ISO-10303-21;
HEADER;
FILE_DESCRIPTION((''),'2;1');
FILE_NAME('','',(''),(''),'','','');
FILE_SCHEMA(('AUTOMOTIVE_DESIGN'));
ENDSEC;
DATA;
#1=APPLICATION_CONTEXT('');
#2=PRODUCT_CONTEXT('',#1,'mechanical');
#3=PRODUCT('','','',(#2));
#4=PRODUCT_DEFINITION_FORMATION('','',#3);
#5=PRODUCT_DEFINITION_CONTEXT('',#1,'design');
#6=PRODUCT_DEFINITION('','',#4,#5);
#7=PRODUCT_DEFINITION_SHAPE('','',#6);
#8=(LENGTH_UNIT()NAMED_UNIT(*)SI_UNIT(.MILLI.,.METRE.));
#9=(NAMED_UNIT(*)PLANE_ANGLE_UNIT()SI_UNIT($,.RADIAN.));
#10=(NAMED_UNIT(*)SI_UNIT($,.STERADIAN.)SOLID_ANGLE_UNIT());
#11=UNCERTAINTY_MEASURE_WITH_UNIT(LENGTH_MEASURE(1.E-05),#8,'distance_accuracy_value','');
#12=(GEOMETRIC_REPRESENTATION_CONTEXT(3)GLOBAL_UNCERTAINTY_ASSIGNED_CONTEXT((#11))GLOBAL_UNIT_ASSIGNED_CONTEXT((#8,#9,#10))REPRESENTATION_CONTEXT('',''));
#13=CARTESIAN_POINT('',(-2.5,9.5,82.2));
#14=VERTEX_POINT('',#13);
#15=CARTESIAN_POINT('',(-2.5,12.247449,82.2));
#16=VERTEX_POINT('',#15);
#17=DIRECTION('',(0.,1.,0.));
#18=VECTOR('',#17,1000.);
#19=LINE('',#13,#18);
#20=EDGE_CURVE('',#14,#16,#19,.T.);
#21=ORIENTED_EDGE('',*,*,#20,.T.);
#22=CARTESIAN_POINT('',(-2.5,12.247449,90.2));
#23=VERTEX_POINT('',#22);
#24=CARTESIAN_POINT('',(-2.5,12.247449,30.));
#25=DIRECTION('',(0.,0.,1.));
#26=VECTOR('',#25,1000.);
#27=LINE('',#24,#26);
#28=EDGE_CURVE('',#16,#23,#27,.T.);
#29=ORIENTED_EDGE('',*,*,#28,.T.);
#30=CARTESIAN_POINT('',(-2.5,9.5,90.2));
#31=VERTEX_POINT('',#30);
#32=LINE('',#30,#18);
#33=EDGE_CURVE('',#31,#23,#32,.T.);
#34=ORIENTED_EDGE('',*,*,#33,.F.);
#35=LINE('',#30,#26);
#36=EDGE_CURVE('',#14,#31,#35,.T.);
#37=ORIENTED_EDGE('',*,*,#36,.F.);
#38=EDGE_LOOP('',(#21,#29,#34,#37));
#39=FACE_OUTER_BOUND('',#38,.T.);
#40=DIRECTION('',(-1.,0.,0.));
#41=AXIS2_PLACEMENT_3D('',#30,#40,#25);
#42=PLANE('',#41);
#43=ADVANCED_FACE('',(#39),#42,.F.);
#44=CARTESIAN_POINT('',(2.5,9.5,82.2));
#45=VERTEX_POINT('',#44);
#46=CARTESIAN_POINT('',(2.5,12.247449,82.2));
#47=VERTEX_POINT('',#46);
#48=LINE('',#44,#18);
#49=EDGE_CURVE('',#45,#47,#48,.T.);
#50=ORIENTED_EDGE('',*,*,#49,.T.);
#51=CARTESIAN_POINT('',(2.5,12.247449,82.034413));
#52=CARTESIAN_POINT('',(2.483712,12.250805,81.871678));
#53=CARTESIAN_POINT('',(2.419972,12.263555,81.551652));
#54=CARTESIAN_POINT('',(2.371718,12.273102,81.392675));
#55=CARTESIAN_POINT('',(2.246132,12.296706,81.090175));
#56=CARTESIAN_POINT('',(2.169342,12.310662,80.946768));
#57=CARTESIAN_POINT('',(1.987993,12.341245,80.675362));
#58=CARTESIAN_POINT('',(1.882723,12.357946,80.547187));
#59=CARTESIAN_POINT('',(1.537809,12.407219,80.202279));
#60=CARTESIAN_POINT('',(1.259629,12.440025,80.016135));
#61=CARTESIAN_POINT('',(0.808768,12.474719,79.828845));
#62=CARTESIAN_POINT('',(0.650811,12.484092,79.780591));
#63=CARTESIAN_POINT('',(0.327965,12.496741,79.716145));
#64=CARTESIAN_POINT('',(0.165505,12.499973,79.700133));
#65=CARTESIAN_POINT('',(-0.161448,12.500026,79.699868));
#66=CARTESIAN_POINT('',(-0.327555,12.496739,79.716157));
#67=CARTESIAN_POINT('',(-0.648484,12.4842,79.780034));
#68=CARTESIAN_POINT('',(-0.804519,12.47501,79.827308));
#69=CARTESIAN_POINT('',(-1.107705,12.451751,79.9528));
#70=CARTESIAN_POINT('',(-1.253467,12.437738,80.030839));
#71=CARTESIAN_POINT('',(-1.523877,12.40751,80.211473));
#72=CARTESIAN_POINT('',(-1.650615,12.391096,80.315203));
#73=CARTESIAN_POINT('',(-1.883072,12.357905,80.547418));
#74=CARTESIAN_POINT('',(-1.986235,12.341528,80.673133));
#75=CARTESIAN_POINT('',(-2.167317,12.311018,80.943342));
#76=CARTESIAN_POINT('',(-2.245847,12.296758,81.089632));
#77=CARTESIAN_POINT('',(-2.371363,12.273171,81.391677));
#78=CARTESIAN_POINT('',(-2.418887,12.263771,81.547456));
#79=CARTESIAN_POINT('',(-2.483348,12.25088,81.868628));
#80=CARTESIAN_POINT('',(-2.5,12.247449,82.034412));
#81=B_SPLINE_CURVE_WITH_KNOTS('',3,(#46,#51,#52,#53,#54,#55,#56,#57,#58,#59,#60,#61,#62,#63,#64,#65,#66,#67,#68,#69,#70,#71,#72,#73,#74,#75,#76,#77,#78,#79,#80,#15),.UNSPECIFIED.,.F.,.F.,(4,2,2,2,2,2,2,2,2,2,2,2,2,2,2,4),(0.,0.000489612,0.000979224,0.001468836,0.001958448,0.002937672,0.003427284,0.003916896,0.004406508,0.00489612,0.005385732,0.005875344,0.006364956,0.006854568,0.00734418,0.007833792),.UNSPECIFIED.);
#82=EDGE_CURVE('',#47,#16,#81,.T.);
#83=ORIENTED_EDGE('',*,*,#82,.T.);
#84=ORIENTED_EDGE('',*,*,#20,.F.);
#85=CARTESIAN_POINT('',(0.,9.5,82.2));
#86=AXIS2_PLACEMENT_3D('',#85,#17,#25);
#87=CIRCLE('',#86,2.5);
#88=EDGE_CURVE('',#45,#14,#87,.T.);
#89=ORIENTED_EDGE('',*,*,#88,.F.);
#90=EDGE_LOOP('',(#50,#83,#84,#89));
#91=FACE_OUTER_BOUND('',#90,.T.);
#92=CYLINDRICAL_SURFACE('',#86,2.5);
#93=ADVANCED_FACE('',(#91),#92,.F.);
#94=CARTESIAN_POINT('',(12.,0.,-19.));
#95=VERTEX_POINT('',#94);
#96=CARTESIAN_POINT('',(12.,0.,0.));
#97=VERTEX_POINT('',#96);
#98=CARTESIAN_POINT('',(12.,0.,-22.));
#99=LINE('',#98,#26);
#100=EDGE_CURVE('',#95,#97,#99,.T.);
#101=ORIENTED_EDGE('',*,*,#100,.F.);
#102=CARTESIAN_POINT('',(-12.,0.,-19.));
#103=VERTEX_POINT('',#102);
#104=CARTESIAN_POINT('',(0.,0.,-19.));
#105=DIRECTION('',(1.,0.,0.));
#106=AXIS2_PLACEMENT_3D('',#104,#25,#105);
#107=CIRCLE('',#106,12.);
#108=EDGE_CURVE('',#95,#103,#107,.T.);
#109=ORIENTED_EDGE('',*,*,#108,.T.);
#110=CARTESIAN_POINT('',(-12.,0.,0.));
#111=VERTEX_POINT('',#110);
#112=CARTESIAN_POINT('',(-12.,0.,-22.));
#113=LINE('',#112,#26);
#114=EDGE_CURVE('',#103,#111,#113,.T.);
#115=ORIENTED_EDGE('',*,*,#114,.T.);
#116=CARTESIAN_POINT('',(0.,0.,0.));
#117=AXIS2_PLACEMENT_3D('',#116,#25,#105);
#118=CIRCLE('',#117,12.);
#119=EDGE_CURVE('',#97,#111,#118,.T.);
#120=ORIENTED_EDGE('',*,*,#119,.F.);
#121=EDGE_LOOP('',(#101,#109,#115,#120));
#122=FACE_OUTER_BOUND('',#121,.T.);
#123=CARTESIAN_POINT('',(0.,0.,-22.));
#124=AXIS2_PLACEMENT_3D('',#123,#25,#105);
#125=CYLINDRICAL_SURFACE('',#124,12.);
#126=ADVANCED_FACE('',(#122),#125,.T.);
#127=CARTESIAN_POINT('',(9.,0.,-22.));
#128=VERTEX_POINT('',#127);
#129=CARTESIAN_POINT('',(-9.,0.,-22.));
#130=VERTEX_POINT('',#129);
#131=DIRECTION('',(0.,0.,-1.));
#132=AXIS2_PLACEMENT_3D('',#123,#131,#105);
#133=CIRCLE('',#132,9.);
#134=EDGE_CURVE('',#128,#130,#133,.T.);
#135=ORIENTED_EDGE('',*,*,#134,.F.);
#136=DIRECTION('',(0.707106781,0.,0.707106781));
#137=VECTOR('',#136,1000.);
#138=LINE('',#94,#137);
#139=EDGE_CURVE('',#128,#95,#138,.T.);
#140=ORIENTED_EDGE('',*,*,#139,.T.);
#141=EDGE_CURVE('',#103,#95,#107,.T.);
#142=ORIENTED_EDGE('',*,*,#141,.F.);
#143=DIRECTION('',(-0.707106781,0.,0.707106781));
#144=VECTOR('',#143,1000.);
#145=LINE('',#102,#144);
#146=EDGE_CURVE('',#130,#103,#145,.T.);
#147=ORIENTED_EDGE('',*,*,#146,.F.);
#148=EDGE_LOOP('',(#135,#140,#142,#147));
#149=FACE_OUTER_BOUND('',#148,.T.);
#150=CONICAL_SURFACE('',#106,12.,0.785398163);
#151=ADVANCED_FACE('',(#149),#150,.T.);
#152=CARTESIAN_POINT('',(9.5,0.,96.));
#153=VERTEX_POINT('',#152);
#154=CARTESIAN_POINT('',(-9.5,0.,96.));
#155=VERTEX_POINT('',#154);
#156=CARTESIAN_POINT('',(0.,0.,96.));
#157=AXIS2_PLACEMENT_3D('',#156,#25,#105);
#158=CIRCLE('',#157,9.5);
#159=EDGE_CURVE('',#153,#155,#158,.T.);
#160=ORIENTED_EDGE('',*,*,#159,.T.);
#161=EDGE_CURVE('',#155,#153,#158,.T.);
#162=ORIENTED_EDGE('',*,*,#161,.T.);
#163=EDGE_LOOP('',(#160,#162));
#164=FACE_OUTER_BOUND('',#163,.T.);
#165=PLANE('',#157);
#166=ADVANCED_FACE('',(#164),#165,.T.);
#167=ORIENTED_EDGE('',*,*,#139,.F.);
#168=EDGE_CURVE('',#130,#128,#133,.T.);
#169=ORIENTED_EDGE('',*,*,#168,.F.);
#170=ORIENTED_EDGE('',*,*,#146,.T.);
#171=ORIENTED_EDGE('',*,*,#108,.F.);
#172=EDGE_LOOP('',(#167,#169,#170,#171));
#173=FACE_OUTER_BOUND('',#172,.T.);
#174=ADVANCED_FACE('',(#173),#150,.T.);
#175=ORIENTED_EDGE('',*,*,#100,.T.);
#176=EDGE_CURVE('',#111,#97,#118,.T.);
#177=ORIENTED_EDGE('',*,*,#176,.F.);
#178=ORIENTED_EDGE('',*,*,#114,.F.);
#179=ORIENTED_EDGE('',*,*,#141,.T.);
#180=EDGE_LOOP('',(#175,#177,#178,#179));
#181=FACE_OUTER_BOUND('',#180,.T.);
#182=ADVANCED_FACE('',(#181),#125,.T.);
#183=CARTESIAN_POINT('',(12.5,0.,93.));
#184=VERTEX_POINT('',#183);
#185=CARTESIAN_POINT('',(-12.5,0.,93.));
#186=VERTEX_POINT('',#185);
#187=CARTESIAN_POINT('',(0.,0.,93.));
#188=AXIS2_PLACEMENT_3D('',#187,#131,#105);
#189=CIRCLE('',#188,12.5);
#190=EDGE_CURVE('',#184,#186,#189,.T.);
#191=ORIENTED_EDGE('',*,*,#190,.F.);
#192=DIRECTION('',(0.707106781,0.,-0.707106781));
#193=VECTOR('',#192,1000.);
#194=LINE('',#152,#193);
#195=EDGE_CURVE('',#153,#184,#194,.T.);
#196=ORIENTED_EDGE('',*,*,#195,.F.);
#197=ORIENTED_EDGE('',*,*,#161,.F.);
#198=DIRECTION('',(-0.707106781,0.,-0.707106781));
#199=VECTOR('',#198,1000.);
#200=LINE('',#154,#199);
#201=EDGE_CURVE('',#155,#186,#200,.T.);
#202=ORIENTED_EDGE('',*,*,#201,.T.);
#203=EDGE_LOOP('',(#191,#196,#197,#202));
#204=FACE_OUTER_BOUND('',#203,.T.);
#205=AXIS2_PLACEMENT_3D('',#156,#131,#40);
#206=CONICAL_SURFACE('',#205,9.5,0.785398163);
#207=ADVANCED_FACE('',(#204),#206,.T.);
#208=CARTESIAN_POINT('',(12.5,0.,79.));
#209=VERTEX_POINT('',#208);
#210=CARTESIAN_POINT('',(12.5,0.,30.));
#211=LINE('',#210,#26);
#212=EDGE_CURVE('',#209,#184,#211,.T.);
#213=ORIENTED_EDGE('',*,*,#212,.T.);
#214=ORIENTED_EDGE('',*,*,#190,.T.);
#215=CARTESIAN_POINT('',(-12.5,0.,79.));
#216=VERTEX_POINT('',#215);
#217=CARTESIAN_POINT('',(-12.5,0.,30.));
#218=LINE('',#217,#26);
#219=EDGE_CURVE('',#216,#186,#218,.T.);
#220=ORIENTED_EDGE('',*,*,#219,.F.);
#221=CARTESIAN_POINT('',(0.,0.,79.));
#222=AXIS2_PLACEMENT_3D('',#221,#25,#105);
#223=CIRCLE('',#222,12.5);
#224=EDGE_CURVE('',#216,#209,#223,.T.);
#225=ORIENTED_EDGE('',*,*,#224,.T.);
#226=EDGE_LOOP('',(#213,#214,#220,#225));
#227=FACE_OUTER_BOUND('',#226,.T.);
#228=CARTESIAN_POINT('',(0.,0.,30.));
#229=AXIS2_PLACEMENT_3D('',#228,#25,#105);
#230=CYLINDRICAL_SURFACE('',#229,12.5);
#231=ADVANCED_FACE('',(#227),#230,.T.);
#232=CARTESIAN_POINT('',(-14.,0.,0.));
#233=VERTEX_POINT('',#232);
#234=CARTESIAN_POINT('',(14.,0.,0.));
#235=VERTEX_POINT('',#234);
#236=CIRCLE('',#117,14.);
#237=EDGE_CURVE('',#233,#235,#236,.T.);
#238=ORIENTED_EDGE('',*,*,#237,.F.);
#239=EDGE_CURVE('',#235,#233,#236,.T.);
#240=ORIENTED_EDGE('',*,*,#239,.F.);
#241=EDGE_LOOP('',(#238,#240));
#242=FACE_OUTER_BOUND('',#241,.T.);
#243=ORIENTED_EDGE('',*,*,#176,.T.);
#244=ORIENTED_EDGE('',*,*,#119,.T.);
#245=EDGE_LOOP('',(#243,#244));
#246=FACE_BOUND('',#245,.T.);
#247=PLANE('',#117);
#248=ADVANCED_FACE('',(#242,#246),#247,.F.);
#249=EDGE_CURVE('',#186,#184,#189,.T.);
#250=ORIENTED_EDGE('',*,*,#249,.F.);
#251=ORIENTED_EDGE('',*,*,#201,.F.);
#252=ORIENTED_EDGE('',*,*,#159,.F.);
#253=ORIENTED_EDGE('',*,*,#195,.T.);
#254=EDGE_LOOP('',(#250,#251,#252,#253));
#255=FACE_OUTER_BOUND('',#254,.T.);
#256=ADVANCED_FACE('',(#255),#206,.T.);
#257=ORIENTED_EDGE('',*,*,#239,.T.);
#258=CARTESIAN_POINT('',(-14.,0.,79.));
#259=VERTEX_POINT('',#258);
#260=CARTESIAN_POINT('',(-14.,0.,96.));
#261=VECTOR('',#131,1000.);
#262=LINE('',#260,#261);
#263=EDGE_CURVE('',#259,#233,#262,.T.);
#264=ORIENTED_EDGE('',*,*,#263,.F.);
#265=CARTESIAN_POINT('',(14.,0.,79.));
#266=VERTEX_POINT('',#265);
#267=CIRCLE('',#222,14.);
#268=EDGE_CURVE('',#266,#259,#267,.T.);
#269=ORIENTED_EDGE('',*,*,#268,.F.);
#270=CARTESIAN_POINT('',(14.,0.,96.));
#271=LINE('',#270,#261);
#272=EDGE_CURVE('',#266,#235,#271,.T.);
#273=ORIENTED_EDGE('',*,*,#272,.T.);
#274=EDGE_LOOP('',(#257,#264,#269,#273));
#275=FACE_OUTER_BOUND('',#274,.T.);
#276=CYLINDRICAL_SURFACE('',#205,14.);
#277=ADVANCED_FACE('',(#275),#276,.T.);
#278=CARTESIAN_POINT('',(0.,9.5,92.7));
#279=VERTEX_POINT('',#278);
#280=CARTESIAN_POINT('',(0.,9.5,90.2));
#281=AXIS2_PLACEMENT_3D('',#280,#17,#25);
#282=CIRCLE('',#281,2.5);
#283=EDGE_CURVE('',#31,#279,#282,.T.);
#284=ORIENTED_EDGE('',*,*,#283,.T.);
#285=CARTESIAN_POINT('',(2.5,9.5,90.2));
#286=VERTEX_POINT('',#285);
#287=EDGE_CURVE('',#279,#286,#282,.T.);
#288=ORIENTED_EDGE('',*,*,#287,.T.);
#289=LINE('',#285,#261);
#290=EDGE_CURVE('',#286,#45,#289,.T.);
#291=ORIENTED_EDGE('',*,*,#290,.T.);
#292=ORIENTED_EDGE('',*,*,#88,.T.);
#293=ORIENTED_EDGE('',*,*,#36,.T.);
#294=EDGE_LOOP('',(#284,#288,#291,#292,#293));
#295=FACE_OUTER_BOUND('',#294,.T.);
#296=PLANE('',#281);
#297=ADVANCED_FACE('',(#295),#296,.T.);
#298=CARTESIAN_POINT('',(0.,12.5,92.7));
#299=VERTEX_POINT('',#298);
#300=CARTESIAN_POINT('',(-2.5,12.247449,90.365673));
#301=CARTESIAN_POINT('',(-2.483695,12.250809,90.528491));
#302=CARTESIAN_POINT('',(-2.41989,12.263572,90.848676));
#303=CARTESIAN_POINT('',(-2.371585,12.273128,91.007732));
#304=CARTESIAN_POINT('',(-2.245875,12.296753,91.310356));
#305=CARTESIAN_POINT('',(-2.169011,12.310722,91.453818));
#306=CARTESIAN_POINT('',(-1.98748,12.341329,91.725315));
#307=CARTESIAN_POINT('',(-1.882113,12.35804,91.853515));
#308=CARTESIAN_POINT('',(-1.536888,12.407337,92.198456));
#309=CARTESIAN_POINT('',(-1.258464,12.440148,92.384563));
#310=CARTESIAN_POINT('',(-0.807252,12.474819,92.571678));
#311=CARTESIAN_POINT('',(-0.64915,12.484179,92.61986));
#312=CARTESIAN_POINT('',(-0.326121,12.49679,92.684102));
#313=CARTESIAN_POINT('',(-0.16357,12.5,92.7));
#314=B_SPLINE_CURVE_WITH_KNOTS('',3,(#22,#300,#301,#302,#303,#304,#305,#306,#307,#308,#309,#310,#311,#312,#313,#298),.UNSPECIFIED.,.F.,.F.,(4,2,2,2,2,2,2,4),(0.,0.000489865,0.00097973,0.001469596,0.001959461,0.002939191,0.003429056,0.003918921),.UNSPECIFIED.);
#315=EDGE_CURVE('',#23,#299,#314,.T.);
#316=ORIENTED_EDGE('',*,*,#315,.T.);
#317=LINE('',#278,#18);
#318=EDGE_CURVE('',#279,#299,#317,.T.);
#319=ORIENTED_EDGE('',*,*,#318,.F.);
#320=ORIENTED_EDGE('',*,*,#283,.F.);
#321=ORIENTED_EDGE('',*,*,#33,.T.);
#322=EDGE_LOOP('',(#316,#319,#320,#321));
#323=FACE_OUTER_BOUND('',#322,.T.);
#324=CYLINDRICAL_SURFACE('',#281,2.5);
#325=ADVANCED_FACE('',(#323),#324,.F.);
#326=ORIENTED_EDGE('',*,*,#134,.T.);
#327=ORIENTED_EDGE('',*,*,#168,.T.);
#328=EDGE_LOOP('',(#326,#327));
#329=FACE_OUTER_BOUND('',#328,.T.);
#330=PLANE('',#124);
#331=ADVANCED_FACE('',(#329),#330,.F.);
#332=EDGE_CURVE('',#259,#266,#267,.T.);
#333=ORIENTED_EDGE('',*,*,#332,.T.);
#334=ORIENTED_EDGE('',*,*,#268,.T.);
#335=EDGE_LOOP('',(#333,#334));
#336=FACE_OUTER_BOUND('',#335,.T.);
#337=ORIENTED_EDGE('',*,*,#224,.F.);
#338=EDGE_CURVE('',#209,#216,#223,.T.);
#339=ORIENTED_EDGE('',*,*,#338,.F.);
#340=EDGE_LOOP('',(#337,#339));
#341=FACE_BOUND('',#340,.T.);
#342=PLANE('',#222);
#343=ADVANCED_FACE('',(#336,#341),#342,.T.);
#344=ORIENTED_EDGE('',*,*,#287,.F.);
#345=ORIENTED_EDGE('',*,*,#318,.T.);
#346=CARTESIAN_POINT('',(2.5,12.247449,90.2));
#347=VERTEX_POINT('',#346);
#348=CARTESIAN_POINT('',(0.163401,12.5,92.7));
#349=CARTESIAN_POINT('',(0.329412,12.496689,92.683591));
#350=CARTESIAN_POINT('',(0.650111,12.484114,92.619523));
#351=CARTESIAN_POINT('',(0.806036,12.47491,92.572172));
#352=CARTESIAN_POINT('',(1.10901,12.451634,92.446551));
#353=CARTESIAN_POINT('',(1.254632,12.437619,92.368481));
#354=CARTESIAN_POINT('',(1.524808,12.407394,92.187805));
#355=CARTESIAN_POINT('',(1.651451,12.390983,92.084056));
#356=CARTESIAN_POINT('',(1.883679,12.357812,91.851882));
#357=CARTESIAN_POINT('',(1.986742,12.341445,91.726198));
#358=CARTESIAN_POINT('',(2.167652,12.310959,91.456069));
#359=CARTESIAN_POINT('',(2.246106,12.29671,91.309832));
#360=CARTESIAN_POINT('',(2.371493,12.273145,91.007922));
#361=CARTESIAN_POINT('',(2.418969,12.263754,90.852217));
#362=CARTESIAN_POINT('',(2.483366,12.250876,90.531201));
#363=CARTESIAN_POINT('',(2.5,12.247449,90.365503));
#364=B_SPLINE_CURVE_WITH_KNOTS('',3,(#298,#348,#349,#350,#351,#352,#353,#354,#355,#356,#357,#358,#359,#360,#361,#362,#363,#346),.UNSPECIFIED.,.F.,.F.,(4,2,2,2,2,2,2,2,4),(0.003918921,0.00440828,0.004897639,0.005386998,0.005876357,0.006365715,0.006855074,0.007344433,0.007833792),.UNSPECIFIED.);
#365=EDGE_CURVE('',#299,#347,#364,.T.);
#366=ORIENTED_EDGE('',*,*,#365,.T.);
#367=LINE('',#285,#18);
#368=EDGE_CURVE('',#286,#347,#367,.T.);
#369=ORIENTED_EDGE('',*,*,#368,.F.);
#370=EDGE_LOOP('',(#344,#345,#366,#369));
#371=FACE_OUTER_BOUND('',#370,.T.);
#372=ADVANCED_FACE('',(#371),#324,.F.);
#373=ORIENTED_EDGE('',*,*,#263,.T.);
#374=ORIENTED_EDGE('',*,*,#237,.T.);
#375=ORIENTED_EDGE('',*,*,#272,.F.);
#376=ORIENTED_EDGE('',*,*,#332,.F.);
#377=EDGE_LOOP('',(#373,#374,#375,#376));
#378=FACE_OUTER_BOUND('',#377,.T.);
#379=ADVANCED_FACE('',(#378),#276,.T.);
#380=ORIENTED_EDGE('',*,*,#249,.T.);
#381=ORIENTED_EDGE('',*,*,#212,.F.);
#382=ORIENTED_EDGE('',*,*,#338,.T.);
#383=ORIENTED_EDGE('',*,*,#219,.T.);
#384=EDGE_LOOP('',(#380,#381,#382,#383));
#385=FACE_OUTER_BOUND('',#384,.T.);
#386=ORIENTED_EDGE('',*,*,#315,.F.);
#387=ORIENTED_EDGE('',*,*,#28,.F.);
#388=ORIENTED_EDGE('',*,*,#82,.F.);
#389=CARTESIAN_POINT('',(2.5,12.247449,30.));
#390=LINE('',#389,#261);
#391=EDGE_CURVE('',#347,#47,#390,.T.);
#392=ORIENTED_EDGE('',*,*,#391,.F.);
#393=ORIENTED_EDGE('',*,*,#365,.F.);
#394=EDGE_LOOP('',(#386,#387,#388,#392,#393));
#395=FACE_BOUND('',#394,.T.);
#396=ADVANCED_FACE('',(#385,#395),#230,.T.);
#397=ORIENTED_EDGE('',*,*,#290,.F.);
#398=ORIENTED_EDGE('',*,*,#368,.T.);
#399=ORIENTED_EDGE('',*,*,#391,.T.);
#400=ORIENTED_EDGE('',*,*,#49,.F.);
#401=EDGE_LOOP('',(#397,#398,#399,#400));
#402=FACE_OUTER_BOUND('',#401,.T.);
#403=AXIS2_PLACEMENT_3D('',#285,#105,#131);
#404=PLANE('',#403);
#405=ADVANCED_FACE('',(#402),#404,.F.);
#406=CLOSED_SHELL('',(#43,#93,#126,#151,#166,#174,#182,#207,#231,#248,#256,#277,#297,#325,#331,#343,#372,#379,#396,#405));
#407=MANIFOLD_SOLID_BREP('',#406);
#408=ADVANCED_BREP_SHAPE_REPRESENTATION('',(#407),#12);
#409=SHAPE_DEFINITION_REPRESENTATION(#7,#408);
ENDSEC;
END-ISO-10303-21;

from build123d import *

# Parameters (mm, degrees)
SKETCH1_R           = 12
BOSS_EXTRUDE1_DEPTH = 22
SKETCH2_R           = 14
BOSS_EXTRUDE2_DEPTH = 96
CUT_EXTRUDE1_START  = -66
SKETCH3_R           = 14
SKETCH3_R_2         = 12.5
CUT_EXTRUDE1_DEPTH  = 66
CHAMFER1_SIZE       = 3
MOVE_FACE1_BY       = 49
CUT_EXTRUDE2_DEPTH  = 3


with BuildPart() as part:
    # Sketch1 → Boss-Extrude1 (new body)
    with BuildSketch(Plane.XY):
        Circle(SKETCH1_R)
    extrude(amount=-BOSS_EXTRUDE1_DEPTH)

    # Sketch2 → Boss-Extrude2 (add)
    with BuildSketch(Plane.XY):
        Circle(SKETCH2_R)
    extrude(amount=BOSS_EXTRUDE2_DEPTH)

    # Sketch3 → Cut-Extrude1 (cut)
    with BuildSketch(Plane.XY.offset(96).offset(CUT_EXTRUDE1_START)):
        Circle(SKETCH3_R)
        Circle(SKETCH3_R_2, mode=Mode.SUBTRACT)
    extrude(amount=CUT_EXTRUDE1_DEPTH, mode=Mode.SUBTRACT)

    # Chamfer1
    chamfer1_edges = [part.edges().sort_by_distance(p)[0] for p in [
        (-12.5, 0, 96),
        (-12, 0, -22),
    ]]
    chamfer(chamfer1_edges, length=CHAMFER1_SIZE)

    # Move Face1: a face moved outward by 49.0
    extrude(part.faces().sort_by_distance((-7, -11.2, 30))[0], amount=MOVE_FACE1_BY, dir=(0, 0, 1))

    # Sketch4 → Cut-Extrude2 (cut)
    with BuildSketch(Plane(origin=(0, 12.5, 0), x_dir=(1, 0, 0), z_dir=(0, 1, 0))):
        with BuildLine():
            Line((-2.5, -90.2), (-2.5, -82.2))
            ThreePointArc((-2.5, -82.2), (0, -79.7), (2.5, -82.2))
            Line((2.5, -82.2), (2.5, -90.2))
            ThreePointArc((2.5, -90.2), (0, -92.7), (-2.5, -90.2))
        make_face()
    extrude(amount=-CUT_EXTRUDE2_DEPTH, mode=Mode.SUBTRACT)


solid = part.part
